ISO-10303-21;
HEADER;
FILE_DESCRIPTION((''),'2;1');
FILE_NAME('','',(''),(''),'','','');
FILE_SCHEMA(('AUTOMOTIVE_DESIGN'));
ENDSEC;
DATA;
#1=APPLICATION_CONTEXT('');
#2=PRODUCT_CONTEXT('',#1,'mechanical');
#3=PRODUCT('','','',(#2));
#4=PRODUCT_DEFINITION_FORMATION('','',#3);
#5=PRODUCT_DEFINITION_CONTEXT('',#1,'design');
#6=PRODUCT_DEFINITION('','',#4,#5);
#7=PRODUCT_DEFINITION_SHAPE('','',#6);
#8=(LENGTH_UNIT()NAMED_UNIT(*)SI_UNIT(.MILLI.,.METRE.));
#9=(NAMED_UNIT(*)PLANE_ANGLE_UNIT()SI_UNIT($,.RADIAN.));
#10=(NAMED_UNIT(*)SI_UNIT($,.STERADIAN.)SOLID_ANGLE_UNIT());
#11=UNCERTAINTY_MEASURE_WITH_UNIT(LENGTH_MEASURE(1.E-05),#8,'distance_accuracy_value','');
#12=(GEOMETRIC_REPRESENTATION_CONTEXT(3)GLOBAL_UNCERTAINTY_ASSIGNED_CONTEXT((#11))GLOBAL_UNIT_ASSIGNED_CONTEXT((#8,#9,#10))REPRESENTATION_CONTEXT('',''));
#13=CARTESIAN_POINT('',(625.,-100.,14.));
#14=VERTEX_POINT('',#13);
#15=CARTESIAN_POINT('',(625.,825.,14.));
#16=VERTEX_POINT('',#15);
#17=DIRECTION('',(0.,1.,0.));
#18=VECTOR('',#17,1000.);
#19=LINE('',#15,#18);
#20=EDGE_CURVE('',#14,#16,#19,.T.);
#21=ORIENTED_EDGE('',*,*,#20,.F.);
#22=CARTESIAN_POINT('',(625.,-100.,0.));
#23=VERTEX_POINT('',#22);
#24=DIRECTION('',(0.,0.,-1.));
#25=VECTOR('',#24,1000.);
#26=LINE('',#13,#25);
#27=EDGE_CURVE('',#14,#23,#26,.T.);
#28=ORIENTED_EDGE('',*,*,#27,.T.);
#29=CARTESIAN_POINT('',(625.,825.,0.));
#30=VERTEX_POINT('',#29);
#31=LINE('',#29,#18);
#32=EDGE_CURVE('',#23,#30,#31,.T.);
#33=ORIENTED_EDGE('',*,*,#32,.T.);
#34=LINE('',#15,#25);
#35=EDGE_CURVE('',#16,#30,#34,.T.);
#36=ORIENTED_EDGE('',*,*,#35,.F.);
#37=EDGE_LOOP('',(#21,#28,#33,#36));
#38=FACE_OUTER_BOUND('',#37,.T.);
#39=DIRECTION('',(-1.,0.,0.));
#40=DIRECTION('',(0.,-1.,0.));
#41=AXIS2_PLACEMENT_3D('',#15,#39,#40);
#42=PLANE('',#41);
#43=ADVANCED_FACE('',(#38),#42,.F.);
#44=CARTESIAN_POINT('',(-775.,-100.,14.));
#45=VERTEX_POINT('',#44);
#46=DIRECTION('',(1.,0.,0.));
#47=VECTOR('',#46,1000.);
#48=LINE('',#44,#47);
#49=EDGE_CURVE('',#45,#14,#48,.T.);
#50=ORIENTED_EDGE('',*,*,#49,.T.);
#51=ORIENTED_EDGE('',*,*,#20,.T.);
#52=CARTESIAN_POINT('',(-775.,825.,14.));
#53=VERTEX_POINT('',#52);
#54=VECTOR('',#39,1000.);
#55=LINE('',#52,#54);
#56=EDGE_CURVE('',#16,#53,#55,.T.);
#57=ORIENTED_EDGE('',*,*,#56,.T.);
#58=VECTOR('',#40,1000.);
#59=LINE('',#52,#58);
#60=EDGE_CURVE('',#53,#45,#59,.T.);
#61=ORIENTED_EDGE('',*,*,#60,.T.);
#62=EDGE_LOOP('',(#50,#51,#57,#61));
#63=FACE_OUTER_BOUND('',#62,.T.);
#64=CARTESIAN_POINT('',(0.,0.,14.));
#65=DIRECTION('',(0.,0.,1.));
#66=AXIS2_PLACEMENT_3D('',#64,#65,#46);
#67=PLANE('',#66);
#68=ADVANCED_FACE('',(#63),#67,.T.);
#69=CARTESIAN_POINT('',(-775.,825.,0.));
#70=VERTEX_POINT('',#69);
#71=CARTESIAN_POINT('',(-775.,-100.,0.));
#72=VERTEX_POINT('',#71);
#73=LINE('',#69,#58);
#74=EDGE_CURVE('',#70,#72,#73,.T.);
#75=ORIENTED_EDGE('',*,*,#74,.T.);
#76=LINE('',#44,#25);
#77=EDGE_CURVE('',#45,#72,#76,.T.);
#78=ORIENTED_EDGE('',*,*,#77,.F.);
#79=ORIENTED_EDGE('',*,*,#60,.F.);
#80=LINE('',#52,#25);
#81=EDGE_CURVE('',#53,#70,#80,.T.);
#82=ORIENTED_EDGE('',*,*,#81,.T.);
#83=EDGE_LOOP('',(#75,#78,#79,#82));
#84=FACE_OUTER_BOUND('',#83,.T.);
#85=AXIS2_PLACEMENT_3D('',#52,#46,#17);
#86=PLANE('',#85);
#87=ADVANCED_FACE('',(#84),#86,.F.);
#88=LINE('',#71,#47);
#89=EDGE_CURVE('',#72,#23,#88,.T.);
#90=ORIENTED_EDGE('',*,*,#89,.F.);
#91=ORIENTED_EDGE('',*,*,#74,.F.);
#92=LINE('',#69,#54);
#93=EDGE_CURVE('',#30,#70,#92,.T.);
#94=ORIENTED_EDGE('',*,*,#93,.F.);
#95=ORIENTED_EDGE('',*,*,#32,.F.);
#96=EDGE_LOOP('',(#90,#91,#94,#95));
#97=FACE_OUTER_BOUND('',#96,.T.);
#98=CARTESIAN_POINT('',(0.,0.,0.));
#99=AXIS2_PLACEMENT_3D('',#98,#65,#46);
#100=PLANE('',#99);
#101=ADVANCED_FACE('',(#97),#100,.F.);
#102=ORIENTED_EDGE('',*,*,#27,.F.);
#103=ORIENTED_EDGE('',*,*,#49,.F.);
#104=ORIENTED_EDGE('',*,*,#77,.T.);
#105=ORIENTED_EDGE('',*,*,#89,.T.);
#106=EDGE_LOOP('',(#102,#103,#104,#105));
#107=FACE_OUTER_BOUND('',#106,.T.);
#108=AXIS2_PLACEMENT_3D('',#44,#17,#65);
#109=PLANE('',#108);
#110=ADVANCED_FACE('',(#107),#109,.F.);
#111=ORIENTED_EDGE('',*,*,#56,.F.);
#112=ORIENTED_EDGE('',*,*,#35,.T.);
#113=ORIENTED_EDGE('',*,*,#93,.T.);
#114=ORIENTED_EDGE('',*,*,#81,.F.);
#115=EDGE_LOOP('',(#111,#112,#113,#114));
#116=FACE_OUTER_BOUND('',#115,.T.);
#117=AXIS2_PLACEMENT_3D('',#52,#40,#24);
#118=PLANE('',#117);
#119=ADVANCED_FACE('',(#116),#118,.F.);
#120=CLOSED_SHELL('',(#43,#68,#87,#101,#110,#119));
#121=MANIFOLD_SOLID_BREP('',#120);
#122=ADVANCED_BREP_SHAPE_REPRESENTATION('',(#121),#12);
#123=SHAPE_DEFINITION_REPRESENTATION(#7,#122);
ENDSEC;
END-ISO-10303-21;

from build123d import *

# Parameters (mm, degrees)
SKETCH_1_W      = 1400
SKETCH_1_H      = 925
EXTRUDE_1_DEPTH = 14


with BuildPart() as part:
    # 草图1 → 凸台-拉伸1 (new body)
    with BuildSketch(Plane.XY):
        with Locations((-75, 362.5)):
            Rectangle(SKETCH_1_W, SKETCH_1_H)
    extrude(amount=EXTRUDE_1_DEPTH)


solid = part.part
